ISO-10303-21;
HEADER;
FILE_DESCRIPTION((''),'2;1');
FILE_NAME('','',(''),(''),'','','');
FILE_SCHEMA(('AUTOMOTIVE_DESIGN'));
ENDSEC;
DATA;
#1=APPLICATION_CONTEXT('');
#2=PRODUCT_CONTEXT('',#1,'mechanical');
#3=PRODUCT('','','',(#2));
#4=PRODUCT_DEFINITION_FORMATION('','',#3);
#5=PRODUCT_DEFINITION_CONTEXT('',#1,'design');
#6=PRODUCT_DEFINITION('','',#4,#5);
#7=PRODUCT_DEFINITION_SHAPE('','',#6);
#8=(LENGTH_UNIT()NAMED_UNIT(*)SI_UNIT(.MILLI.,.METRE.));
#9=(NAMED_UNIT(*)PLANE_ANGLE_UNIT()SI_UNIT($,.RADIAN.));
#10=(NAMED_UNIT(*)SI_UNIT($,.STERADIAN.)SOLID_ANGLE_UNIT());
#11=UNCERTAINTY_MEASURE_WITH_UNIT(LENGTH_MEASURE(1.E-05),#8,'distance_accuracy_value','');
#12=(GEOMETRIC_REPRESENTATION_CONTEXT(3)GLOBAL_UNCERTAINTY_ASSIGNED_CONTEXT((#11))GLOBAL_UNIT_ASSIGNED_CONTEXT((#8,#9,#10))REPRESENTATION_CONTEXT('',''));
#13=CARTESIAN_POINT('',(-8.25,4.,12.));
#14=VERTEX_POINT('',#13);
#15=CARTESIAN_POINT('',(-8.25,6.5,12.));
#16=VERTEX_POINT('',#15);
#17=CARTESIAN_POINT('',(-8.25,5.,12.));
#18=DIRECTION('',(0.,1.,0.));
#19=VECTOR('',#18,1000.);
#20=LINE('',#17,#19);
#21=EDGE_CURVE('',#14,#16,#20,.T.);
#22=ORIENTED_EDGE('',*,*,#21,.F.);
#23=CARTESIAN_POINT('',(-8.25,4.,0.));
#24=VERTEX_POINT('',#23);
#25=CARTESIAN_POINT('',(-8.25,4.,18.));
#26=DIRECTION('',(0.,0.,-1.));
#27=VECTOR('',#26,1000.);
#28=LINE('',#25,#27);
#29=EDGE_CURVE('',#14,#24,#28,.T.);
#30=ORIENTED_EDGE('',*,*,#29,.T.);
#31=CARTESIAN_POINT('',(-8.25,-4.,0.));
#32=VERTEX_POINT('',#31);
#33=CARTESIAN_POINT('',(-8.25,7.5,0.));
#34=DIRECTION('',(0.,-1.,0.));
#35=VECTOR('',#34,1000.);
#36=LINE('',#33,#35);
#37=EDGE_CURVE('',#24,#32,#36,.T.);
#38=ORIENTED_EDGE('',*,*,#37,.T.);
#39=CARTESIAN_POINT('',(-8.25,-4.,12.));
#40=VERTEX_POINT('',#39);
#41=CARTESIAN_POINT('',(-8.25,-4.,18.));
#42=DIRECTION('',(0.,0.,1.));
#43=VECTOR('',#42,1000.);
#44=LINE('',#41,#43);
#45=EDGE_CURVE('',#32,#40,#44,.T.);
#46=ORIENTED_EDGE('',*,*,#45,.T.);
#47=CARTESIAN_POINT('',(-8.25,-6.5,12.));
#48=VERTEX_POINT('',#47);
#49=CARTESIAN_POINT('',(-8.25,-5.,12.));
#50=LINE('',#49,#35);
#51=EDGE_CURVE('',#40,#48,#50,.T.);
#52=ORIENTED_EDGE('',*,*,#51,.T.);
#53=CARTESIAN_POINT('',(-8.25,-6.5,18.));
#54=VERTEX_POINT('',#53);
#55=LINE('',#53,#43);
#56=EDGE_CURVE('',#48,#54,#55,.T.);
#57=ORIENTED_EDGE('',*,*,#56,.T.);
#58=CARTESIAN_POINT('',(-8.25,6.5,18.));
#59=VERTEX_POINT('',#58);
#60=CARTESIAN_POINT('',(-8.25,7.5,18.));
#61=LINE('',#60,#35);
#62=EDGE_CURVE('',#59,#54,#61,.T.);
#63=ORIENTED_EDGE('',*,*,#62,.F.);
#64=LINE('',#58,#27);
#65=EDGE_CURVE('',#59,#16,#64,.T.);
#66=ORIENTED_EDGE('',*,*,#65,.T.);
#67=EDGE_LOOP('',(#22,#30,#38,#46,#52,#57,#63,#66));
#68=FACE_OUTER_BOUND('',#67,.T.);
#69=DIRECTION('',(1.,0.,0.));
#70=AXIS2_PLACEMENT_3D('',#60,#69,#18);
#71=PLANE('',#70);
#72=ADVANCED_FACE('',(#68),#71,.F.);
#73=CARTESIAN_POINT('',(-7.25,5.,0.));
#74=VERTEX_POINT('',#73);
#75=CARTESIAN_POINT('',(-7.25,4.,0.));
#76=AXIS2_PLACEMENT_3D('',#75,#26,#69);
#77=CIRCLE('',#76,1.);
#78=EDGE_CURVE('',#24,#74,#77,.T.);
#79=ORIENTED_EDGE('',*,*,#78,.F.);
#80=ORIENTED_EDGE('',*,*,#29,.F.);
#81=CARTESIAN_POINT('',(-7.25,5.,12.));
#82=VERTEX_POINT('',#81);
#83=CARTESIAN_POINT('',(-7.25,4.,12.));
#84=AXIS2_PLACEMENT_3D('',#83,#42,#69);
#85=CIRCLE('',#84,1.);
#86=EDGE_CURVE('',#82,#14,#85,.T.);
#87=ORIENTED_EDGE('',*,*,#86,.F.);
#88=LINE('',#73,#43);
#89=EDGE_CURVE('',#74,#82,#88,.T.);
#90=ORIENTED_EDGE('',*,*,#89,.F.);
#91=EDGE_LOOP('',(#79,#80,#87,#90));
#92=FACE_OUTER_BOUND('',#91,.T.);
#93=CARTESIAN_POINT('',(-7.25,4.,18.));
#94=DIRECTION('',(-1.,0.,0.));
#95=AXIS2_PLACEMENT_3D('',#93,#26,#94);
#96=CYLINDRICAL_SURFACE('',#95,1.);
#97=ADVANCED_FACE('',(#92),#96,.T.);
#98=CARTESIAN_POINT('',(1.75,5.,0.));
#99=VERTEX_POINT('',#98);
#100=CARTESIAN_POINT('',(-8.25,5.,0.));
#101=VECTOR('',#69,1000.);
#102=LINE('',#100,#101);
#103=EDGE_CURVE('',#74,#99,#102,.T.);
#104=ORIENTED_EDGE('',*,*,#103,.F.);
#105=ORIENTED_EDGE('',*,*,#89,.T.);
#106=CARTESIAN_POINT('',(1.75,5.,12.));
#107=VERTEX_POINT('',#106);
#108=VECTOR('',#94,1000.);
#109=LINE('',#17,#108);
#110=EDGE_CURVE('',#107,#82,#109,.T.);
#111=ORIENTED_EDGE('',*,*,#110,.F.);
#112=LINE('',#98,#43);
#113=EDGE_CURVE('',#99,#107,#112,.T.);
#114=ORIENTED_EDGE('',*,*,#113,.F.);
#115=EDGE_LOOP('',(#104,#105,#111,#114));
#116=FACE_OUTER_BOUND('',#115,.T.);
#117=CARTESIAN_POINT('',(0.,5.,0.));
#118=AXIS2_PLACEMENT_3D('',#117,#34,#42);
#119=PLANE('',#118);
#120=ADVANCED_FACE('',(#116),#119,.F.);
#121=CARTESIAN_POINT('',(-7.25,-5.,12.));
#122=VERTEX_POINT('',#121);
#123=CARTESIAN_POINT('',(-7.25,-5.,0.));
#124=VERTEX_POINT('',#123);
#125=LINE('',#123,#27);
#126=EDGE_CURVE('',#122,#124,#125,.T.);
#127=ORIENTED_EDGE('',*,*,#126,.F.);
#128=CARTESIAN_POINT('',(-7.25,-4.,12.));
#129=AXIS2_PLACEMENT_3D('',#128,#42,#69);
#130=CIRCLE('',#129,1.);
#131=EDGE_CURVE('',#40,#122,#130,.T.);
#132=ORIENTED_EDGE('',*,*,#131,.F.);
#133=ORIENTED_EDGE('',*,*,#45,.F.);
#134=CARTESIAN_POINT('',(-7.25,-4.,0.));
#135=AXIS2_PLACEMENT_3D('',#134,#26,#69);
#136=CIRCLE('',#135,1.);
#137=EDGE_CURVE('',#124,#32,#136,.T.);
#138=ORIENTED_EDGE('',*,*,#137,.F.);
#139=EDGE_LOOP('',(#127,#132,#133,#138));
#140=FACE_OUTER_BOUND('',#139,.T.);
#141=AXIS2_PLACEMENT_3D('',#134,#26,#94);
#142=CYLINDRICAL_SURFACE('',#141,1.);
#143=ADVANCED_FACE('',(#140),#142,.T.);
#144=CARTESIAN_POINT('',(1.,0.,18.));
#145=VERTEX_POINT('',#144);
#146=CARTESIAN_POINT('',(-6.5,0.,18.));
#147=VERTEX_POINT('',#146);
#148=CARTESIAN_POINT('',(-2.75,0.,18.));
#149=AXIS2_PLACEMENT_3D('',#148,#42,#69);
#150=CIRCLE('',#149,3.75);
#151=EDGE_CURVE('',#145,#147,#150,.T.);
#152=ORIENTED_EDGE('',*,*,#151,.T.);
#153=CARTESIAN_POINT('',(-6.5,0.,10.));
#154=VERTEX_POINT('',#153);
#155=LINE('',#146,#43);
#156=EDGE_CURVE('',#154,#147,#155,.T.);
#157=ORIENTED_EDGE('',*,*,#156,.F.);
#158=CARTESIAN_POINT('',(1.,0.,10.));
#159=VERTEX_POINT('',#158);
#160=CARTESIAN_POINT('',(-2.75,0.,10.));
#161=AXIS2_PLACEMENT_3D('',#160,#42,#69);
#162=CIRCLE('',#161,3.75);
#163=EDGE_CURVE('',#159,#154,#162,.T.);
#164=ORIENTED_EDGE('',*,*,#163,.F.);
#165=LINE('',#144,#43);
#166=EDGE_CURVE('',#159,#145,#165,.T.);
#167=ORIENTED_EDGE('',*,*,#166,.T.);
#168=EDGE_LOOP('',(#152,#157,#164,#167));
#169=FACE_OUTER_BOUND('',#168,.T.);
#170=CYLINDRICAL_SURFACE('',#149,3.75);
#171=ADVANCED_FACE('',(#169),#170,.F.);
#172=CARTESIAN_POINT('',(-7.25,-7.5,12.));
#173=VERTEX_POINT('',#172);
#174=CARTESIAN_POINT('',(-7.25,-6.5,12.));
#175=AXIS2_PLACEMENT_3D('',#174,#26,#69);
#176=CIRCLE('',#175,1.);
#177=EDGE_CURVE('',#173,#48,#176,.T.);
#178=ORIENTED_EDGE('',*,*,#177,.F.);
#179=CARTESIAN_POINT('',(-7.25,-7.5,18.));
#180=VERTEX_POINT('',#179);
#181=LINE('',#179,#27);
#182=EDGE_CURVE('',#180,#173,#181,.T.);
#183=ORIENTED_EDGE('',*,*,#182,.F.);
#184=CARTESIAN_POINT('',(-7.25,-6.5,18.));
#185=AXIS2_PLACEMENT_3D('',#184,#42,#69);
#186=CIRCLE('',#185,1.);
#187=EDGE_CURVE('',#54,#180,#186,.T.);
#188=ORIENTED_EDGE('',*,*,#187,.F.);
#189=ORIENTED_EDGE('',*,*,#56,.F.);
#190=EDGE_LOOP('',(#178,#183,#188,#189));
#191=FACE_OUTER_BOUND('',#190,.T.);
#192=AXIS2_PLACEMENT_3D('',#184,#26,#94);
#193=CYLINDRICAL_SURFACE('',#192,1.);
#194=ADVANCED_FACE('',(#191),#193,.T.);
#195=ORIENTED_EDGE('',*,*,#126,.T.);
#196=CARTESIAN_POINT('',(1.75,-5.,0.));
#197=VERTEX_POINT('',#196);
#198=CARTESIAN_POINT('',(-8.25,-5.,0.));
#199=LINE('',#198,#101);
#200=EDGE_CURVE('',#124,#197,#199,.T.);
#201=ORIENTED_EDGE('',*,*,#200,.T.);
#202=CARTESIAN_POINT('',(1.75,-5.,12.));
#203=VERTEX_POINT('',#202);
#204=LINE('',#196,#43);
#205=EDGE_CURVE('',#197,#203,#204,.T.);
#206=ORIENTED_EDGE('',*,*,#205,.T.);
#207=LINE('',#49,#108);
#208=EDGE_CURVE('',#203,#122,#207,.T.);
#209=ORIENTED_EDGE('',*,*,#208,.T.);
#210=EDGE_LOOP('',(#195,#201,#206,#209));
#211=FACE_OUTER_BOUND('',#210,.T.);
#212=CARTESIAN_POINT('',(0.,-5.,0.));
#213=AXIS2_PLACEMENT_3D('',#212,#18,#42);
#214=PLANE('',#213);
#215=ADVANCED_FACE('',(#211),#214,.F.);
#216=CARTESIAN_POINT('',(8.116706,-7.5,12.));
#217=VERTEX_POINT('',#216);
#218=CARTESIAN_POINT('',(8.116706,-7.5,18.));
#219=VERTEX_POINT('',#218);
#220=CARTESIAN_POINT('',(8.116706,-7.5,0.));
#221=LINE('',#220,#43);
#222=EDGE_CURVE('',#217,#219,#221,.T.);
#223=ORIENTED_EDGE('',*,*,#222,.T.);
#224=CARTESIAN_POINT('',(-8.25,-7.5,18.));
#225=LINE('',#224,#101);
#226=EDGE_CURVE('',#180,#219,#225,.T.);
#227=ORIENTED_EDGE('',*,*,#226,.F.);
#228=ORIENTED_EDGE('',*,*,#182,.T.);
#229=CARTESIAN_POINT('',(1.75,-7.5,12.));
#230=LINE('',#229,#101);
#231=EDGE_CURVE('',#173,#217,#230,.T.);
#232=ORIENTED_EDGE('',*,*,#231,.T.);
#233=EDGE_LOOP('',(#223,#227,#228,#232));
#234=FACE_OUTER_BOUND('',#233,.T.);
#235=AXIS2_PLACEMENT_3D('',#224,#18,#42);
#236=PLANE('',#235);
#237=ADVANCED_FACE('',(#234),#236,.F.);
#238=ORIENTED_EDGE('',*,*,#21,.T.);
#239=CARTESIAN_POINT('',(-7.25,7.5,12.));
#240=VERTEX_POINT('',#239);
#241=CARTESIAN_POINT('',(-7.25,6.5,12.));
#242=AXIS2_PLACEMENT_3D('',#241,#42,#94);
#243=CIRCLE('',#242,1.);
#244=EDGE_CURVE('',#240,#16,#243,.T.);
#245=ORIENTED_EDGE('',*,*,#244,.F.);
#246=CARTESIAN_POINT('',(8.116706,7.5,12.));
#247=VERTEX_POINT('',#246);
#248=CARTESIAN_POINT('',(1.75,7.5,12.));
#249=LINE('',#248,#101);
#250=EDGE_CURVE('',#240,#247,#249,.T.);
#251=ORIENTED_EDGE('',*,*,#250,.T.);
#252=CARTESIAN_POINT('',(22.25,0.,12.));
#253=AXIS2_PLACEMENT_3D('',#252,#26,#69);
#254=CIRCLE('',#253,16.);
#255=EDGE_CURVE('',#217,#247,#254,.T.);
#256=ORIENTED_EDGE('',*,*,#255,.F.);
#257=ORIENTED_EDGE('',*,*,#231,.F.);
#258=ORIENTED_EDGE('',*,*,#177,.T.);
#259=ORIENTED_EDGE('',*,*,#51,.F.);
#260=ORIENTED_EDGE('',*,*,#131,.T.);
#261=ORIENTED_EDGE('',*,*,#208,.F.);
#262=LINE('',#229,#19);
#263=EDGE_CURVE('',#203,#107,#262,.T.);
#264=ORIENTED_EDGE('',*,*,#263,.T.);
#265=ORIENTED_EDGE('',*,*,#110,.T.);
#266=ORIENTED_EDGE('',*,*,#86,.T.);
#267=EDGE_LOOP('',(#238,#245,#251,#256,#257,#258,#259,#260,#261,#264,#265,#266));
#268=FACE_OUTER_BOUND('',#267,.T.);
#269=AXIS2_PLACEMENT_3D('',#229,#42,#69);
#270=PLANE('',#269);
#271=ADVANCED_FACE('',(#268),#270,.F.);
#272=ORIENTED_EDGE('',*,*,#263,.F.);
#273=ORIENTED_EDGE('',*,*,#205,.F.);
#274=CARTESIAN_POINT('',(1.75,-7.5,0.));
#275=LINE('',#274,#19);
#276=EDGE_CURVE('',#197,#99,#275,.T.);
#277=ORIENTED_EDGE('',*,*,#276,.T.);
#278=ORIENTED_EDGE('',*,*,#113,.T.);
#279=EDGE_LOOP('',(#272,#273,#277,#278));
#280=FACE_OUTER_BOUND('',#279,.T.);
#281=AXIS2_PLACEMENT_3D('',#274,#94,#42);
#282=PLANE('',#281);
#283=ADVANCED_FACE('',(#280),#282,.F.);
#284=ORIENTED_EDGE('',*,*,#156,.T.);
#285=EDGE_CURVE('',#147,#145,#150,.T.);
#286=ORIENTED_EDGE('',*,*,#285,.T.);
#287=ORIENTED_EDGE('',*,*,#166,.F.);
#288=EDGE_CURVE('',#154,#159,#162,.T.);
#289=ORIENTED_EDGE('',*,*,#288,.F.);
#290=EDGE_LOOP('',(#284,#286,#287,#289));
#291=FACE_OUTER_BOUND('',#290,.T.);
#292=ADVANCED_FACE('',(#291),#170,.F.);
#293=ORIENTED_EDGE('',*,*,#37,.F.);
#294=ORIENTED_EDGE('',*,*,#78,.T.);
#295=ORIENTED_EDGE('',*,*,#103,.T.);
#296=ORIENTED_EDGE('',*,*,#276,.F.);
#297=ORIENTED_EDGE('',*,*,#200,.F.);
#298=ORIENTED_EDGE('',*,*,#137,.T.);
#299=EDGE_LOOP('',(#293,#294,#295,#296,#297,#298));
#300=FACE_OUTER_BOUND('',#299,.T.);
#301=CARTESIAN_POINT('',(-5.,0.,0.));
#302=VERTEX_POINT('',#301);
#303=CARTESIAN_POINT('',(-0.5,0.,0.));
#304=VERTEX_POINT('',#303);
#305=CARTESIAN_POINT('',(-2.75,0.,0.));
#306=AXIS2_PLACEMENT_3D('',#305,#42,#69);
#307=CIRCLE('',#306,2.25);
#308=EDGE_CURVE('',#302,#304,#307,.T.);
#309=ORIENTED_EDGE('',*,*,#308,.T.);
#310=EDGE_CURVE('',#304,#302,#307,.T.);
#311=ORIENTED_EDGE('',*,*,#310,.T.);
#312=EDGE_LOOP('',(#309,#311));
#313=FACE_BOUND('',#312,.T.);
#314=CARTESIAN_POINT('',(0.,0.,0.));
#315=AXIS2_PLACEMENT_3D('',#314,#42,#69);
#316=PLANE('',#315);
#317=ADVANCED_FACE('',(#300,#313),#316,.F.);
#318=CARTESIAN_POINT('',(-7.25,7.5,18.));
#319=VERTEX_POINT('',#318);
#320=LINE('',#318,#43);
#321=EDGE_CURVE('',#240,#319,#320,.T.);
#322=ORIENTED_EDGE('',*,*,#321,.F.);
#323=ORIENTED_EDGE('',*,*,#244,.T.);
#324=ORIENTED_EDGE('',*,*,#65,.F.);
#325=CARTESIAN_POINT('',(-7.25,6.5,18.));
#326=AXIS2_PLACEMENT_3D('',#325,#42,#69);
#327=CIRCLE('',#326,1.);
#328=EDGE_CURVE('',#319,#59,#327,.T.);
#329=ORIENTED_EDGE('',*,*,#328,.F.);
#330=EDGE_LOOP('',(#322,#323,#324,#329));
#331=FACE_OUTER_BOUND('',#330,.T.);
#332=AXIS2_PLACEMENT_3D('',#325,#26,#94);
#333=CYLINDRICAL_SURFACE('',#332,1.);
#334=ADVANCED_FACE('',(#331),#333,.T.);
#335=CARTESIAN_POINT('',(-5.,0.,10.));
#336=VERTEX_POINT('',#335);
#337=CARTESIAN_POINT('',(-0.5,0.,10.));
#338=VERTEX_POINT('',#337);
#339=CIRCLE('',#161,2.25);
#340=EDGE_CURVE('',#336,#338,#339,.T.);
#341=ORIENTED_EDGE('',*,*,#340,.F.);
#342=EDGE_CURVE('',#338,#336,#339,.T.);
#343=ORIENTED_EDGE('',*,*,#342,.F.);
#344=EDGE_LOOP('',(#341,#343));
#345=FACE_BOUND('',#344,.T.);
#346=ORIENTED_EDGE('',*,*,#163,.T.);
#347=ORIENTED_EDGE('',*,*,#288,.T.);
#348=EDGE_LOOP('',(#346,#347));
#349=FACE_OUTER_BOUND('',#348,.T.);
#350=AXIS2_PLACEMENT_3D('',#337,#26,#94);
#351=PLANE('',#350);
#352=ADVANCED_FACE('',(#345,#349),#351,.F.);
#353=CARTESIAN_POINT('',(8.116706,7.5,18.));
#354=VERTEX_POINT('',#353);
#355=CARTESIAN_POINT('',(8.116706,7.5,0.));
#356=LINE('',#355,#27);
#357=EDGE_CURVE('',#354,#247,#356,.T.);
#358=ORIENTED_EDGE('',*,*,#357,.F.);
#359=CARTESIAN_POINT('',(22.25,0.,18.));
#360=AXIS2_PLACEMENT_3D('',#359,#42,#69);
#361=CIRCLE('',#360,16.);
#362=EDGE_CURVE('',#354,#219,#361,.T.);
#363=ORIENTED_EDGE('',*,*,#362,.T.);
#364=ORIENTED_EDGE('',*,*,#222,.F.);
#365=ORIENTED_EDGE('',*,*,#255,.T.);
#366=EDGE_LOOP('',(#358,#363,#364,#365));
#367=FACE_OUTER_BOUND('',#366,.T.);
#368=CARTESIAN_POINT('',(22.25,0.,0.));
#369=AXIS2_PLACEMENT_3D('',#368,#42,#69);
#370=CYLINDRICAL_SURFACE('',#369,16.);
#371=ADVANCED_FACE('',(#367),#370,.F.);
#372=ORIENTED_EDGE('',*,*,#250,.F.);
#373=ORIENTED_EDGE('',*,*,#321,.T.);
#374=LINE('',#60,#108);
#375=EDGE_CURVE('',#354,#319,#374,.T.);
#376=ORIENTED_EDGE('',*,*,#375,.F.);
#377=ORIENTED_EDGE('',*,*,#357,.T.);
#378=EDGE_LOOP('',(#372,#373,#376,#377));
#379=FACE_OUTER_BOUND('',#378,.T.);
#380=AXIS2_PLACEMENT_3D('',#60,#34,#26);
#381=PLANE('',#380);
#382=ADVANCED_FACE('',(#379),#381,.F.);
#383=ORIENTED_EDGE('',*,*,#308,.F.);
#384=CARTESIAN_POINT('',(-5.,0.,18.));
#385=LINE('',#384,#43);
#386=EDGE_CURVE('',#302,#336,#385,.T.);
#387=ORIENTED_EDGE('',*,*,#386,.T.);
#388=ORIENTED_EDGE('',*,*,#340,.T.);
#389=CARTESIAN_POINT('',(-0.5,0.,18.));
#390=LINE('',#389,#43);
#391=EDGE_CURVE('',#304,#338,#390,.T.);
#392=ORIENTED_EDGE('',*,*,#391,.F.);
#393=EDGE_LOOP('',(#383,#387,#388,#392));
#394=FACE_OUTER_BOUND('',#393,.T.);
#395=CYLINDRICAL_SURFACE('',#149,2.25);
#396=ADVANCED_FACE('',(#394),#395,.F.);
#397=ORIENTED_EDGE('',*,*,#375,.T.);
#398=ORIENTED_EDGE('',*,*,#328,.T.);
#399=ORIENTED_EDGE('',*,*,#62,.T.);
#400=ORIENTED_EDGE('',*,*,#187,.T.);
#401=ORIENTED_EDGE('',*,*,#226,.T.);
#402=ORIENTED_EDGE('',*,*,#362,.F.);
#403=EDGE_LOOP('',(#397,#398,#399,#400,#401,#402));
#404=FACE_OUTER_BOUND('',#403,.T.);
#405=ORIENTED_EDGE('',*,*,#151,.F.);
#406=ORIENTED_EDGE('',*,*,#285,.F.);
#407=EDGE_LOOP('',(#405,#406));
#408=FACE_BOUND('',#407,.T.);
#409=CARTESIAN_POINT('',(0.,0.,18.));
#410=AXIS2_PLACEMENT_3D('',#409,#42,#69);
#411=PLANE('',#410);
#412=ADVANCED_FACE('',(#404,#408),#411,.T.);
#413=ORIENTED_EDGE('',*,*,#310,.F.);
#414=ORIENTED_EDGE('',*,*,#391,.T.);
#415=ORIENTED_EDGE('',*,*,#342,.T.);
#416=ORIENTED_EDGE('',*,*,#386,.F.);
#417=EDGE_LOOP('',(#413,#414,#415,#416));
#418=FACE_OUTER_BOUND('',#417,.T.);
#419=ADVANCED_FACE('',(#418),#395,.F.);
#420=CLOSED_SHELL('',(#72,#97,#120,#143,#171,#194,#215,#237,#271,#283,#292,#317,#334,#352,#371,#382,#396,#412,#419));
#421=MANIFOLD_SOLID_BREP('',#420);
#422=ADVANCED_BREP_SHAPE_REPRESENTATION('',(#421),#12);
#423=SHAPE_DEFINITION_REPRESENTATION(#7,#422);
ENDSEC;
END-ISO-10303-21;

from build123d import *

# Parameters (mm, degrees)
SKETCH1_W                                           = 16.5
SKETCH1_H                                           = 15
BOSS_EXTRUDE1_DEPTH                                 = 18
FILLET1_R                                           = 1
CBORE_FOR_M4_HEX_SOCKET_HEAD_CAP_SCREW1_D           = 4.5
CBORE_FOR_M4_HEX_SOCKET_HEAD_CAP_SCREW1_CBORE_D     = 7.5
CBORE_FOR_M4_HEX_SOCKET_HEAD_CAP_SCREW1_CBORE_DEPTH = 8
SKETCH7_R                                           = 16
CUT_EXTRUDE2_DEPTH                                  = 22.17339132
SKETCH8_W                                           = 6.5
SKETCH8_H                                           = 12
CUT_EXTRUDE3_DEPTH                                  = 25.840742743
SKETCH9_W                                           = 10
SKETCH9_H                                           = 12
CUT_EXTRUDE4_DEPTH                                  = 2.5
FILLET2_R                                           = 1


with BuildPart() as part:
    # Sketch1 → Boss-Extrude1 (new body)
    with BuildSketch(Plane.XY):
        Rectangle(SKETCH1_W, SKETCH1_H)
    extrude(amount=BOSS_EXTRUDE1_DEPTH)

    # Fillet1
    fillet1_edges = [part.edges().sort_by_distance(p)[0] for p in [
        (-8.25, -7.5, 9),
        (-8.25, 7.5, 9),
    ]]
    fillet(fillet1_edges, radius=FILLET1_R)

    # CBORE for M4 Hex Socket Head Cap Screw1 (through all)
    with Locations(Plane.XY.offset(18)):
        with Locations((-2.75, 0)):
            CounterBoreHole(CBORE_FOR_M4_HEX_SOCKET_HEAD_CAP_SCREW1_D / 2, CBORE_FOR_M4_HEX_SOCKET_HEAD_CAP_SCREW1_CBORE_D / 2, CBORE_FOR_M4_HEX_SOCKET_HEAD_CAP_SCREW1_CBORE_DEPTH)

    # Sketch7 → Cut-Extrude2 (cut, through all)
    with BuildSketch(Plane.XY.offset(18)):
        with Locations((22.25, 0)):
            Circle(SKETCH7_R)
    extrude(amount=-CUT_EXTRUDE2_DEPTH, mode=Mode.SUBTRACT)

    # Sketch8 → Cut-Extrude3 (cut, through all)
    with BuildSketch(Plane(origin=(0, 7.5, 0), x_dir=(1, 0, 0), z_dir=(0, 1, 0))):
        with Locations((5, -6)):
            Rectangle(SKETCH8_W, SKETCH8_H)
    extrude(amount=-CUT_EXTRUDE3_DEPTH, mode=Mode.SUBTRACT)

    # Sketch9 → Cut-Extrude4 (cut)
    with BuildSketch(Plane(origin=(0, -7.5, 0), x_dir=(-1, 0, 0), z_dir=(0, -1, 0))):
        with Locations((3.25, -6)):
            Rectangle(SKETCH9_W, SKETCH9_H)
    cut_extrude4 = extrude(amount=-CUT_EXTRUDE4_DEPTH, mode=Mode.SUBTRACT)

    # Mirror1: Cut-Extrude4 across plane
    add(cut_extrude4.mirror(Plane.ZX), mode=Mode.SUBTRACT)

    # Fillet2
    fillet2_edges = [part.edges().sort_by_distance(p)[0] for p in [
        (-8.25, 5, 6),
        (-8.25, -5, 6),
    ]]
    fillet(fillet2_edges, radius=FILLET2_R)


solid = part.part
